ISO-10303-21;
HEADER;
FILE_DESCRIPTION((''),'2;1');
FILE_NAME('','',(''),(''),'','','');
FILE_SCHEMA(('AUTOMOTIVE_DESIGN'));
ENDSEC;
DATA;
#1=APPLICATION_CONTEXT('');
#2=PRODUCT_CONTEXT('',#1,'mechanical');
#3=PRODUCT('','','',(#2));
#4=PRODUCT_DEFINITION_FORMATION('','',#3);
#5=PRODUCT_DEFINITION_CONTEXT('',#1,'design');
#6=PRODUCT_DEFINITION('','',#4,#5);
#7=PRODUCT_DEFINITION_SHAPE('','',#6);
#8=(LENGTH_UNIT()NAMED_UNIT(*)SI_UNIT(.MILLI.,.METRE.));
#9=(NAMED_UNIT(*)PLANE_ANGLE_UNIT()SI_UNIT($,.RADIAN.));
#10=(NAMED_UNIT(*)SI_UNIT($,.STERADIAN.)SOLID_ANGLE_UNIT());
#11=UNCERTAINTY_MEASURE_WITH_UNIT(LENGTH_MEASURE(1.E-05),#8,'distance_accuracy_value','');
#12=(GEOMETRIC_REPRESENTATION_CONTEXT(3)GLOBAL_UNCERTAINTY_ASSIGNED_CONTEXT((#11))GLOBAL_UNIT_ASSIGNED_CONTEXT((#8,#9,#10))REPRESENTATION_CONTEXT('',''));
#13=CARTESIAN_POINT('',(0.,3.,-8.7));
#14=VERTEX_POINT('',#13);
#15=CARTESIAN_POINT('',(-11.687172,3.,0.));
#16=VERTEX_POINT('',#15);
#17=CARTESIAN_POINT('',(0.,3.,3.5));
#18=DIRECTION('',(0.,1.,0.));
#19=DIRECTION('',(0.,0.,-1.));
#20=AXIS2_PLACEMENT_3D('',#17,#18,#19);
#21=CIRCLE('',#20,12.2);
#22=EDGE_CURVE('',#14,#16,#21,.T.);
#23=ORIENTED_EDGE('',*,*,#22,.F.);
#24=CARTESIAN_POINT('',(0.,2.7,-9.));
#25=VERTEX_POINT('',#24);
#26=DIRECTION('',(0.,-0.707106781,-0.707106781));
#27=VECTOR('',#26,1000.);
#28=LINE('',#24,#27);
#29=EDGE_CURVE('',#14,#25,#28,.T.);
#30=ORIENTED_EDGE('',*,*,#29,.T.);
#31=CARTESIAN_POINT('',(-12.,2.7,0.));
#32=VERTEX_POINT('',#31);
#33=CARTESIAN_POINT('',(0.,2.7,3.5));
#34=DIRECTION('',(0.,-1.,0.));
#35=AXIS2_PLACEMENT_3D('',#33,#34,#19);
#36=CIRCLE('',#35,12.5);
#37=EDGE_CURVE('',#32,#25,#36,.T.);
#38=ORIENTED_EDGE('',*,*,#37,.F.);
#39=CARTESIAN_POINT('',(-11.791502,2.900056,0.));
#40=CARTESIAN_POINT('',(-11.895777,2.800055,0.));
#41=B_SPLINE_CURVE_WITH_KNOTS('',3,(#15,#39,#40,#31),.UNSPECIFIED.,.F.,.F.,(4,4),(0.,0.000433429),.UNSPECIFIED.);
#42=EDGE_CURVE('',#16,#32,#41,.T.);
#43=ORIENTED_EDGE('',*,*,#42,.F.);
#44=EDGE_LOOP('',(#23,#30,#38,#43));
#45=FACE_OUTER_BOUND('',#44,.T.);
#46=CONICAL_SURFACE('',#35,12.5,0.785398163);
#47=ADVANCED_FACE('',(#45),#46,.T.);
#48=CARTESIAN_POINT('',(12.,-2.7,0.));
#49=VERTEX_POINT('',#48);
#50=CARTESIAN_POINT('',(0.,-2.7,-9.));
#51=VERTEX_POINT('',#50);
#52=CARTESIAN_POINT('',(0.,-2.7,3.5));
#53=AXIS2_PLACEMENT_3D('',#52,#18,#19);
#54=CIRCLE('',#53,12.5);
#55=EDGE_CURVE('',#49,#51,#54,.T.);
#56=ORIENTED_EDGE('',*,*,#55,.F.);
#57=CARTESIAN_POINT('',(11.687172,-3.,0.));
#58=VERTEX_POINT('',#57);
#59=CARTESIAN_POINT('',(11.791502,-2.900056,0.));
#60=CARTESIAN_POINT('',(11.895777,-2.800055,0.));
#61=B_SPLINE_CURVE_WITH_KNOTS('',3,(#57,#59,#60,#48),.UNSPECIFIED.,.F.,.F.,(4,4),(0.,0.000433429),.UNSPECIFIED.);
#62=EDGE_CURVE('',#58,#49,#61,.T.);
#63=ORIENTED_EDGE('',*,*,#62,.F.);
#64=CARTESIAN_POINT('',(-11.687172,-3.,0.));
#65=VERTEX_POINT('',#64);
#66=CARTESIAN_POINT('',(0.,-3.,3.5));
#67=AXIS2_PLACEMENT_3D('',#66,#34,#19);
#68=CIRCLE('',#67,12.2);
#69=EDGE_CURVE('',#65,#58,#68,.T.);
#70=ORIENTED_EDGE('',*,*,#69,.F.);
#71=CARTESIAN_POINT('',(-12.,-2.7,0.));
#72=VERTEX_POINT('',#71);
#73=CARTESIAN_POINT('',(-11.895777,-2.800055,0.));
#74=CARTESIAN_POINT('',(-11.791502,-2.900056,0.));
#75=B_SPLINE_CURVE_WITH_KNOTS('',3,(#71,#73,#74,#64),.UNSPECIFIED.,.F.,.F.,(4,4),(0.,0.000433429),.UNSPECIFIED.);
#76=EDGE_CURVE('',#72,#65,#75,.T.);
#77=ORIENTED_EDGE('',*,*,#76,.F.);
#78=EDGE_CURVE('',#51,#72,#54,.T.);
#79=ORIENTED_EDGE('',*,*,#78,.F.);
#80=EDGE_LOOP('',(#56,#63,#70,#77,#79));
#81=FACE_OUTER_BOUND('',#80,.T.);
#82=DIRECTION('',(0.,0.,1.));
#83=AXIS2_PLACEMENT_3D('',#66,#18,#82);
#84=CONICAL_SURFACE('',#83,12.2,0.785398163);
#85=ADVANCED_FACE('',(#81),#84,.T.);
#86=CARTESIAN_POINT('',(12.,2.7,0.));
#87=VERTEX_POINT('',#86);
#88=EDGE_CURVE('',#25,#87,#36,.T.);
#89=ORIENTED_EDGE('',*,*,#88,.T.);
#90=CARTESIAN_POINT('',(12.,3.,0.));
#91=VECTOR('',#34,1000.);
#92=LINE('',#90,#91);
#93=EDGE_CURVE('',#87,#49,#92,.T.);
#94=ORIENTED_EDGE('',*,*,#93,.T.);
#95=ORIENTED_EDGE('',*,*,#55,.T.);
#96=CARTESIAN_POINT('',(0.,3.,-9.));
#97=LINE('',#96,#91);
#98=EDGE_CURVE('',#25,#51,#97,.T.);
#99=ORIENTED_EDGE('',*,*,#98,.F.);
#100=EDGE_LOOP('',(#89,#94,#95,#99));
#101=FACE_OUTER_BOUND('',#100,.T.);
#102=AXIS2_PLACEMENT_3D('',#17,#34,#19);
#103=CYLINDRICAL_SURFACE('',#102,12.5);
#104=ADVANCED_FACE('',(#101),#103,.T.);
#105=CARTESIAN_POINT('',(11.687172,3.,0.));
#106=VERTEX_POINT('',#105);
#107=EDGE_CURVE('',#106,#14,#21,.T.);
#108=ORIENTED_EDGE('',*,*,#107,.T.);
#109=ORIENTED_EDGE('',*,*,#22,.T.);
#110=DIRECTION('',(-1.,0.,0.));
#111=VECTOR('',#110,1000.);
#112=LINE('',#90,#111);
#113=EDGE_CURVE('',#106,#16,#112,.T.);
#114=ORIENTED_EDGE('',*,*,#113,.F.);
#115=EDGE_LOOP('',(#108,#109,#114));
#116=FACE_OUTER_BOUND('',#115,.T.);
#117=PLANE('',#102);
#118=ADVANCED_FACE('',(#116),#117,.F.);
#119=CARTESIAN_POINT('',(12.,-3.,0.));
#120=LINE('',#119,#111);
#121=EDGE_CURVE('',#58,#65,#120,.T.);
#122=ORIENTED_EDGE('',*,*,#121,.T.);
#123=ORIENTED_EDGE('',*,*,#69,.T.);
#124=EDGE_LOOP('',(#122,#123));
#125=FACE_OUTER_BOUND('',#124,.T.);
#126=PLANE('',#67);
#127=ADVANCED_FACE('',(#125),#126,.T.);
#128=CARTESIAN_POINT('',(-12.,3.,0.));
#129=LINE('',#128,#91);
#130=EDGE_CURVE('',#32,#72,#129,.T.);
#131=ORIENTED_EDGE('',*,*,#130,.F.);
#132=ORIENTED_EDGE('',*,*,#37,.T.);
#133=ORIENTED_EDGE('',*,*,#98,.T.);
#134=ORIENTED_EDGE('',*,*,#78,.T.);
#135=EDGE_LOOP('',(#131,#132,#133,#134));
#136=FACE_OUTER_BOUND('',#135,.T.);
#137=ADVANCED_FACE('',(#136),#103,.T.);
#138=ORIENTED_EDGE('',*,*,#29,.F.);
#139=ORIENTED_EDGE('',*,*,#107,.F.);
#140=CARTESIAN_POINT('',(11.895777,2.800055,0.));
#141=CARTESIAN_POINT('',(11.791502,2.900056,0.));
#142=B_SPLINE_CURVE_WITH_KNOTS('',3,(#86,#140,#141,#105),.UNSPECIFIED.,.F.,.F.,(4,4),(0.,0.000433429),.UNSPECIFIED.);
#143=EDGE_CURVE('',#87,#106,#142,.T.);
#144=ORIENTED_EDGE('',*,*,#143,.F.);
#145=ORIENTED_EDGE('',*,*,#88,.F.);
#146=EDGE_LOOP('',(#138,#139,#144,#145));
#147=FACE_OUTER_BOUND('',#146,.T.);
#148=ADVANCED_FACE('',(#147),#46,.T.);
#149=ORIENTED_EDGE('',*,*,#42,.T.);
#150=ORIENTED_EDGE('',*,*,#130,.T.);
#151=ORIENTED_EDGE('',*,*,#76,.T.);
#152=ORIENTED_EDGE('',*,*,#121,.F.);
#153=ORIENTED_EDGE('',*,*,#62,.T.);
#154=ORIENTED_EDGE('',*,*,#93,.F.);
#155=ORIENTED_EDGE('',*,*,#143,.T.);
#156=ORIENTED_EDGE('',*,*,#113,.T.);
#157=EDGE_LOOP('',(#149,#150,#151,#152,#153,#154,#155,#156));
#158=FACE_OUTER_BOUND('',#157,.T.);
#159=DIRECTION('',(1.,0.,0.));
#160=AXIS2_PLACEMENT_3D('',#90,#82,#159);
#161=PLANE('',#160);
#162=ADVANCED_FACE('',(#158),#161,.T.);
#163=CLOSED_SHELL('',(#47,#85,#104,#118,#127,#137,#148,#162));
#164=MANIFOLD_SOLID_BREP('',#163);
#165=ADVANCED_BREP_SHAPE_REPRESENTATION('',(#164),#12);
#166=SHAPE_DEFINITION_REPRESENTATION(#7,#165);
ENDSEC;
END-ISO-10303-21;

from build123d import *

# Parameters (mm, degrees)
BOSS_EXTRUDE1_DEPTH = 6
CHAMFER1_SIZE       = 0.3


with BuildPart() as part:
    # Sketch1 → Boss-Extrude1 (new body)
    with BuildSketch(Plane.XZ.offset(3)):
        with BuildLine():
            Line((12, 0), (-12, 0))
            ThreePointArc((-12, 0), (0, -9), (12, 0))
        make_face()
    extrude(amount=-BOSS_EXTRUDE1_DEPTH)

    # Chamfer1
    chamfer1_edges = [part.edges().sort_by_distance(p)[0] for p in [
        (0, -3, -9),
        (0, 3, -9),
    ]]
    chamfer(chamfer1_edges, length=CHAMFER1_SIZE)


solid = part.part
